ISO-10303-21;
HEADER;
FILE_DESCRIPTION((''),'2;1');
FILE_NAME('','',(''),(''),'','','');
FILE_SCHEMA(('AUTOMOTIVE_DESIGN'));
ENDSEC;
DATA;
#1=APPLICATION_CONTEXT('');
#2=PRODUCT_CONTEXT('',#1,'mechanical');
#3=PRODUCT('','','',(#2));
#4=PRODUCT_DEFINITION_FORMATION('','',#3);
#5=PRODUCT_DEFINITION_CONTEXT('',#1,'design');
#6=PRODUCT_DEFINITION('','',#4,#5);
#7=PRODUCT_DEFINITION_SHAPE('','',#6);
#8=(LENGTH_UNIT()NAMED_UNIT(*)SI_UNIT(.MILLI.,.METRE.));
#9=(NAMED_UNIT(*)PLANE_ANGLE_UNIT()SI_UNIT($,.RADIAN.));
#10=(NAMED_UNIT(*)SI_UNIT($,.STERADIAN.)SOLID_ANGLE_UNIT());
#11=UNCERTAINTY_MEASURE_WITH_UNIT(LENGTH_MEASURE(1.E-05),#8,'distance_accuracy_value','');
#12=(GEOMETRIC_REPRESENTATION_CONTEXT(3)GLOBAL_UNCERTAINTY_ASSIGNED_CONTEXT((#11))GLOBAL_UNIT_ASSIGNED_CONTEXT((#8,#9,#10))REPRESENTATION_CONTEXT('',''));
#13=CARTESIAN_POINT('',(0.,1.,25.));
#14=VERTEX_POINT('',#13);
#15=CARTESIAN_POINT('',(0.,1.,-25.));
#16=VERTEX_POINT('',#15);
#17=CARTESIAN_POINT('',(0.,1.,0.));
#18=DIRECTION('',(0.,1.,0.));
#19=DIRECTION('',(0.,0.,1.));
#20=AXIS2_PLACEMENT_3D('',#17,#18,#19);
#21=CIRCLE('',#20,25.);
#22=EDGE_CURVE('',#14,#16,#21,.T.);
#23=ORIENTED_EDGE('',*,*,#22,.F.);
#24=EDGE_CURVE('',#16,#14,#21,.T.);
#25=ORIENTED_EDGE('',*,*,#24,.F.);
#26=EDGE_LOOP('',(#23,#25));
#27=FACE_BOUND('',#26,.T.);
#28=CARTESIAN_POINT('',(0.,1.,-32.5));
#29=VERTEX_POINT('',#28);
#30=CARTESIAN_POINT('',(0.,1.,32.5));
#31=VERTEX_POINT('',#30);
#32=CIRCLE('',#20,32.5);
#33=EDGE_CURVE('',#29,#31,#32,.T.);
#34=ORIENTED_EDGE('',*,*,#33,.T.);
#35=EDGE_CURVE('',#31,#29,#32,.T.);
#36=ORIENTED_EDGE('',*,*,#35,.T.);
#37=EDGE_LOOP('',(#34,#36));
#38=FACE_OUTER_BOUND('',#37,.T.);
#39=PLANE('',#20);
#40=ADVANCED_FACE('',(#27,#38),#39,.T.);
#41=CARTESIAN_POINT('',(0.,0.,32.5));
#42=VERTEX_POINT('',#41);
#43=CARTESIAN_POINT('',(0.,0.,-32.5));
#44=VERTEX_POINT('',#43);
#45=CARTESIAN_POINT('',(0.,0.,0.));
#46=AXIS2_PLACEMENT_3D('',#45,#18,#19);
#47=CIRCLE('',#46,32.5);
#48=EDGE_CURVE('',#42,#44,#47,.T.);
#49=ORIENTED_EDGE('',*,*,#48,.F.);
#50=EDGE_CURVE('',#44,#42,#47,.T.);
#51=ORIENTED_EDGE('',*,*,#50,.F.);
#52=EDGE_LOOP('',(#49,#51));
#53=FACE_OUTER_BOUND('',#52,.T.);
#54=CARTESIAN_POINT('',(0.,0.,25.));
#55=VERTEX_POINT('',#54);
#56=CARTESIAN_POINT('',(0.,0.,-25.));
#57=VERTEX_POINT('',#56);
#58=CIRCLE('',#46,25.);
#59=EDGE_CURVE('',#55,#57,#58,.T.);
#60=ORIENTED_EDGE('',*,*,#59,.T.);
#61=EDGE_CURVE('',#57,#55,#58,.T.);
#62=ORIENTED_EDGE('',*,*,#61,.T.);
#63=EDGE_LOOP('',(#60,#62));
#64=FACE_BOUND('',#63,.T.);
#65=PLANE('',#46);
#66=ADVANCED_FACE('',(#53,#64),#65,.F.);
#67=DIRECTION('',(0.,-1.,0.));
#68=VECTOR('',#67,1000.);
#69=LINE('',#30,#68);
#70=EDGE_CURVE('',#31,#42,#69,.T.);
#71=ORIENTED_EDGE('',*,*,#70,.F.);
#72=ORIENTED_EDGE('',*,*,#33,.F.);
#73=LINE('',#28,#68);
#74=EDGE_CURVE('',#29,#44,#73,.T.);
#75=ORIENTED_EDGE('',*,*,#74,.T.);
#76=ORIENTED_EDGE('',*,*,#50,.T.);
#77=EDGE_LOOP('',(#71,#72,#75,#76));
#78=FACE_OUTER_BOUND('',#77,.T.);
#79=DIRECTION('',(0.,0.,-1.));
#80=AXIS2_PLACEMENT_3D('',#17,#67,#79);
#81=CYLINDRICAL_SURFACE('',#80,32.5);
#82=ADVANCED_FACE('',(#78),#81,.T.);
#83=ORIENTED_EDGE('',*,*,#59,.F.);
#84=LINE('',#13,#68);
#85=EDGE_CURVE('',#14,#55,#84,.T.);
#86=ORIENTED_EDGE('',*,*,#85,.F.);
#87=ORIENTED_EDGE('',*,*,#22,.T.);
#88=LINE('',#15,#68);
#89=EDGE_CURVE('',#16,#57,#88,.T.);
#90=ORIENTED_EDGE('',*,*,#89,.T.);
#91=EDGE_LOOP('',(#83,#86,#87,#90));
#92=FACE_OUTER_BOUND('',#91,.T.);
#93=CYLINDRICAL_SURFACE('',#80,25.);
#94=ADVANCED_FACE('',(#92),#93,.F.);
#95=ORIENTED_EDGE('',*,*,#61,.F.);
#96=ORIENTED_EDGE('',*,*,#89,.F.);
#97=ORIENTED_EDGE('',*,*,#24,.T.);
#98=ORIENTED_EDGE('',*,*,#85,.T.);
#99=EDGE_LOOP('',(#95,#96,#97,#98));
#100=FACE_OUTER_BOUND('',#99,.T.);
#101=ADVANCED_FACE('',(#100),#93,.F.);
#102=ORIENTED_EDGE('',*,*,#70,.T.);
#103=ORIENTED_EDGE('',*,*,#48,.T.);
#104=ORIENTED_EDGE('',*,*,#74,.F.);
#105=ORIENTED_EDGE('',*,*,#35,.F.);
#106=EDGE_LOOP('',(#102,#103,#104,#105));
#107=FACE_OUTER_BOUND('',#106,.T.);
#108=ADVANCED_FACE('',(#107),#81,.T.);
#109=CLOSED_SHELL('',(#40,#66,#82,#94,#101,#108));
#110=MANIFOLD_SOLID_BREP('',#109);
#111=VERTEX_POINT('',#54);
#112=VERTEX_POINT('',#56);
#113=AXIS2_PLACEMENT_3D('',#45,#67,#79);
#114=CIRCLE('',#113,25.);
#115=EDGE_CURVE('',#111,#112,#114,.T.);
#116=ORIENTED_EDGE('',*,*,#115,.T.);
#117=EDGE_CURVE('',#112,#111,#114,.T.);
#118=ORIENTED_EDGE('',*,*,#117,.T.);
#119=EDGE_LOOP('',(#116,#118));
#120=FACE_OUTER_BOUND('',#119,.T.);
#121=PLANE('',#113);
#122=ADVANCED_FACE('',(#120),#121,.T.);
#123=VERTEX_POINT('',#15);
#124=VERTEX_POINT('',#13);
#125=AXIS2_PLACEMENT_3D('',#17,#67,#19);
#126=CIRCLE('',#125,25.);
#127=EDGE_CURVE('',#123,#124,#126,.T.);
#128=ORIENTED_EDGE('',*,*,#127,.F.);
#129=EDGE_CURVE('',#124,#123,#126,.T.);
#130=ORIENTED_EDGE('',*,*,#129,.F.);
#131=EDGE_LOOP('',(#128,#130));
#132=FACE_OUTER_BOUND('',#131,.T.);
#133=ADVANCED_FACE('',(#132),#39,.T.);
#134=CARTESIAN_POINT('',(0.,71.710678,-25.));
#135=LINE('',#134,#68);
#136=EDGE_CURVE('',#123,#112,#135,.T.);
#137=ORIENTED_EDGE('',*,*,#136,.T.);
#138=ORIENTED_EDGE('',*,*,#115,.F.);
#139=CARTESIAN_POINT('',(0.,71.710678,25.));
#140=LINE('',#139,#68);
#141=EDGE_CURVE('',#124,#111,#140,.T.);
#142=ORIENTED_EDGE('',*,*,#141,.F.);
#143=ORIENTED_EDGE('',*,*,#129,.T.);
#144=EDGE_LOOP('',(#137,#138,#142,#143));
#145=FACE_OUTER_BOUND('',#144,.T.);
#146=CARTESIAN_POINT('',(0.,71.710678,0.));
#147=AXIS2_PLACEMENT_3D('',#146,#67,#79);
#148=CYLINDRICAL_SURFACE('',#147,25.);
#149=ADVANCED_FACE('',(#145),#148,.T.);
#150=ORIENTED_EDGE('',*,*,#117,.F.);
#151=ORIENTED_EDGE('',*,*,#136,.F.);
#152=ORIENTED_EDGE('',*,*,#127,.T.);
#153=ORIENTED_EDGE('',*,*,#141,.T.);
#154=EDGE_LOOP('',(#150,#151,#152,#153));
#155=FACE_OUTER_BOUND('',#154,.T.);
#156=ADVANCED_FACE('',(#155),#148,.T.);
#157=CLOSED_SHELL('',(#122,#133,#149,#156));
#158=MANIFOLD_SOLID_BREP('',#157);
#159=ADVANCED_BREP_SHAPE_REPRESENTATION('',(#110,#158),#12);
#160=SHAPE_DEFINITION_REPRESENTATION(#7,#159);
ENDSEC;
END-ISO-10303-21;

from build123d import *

# Parameters (mm, degrees)
SKETCH1_R           = 32.5
SKETCH1_R_2         = 25
BOSS_EXTRUDE1_DEPTH = 1
SKETCH2_R           = 25
BOSS_EXTRUDE2_DEPTH = 1


with BuildPart() as part:
    # Sketch1 → Boss-Extrude1 (new body)
    with BuildSketch(Plane(origin=(0, 0, 0), x_dir=(1, 0, 0), z_dir=(0, 1, 0))):
        with Locations(Location((0, 0, 0), (0, 0, 270))):
            Circle(SKETCH1_R)
        with Locations(Location((0, 0, 0), (0, 0, 270))):
            Circle(SKETCH1_R_2, mode=Mode.SUBTRACT)
    extrude(amount=BOSS_EXTRUDE1_DEPTH)


with BuildPart() as body_2:
    # Sketch2 → Boss-Extrude2 (new body)
    with BuildSketch(Plane.XZ):
        with Locations(Location((0, 0, 0), (0, 0, 270))):
            Circle(SKETCH2_R)
    extrude(amount=-BOSS_EXTRUDE2_DEPTH)


solid = Compound([part.part, body_2.part])
